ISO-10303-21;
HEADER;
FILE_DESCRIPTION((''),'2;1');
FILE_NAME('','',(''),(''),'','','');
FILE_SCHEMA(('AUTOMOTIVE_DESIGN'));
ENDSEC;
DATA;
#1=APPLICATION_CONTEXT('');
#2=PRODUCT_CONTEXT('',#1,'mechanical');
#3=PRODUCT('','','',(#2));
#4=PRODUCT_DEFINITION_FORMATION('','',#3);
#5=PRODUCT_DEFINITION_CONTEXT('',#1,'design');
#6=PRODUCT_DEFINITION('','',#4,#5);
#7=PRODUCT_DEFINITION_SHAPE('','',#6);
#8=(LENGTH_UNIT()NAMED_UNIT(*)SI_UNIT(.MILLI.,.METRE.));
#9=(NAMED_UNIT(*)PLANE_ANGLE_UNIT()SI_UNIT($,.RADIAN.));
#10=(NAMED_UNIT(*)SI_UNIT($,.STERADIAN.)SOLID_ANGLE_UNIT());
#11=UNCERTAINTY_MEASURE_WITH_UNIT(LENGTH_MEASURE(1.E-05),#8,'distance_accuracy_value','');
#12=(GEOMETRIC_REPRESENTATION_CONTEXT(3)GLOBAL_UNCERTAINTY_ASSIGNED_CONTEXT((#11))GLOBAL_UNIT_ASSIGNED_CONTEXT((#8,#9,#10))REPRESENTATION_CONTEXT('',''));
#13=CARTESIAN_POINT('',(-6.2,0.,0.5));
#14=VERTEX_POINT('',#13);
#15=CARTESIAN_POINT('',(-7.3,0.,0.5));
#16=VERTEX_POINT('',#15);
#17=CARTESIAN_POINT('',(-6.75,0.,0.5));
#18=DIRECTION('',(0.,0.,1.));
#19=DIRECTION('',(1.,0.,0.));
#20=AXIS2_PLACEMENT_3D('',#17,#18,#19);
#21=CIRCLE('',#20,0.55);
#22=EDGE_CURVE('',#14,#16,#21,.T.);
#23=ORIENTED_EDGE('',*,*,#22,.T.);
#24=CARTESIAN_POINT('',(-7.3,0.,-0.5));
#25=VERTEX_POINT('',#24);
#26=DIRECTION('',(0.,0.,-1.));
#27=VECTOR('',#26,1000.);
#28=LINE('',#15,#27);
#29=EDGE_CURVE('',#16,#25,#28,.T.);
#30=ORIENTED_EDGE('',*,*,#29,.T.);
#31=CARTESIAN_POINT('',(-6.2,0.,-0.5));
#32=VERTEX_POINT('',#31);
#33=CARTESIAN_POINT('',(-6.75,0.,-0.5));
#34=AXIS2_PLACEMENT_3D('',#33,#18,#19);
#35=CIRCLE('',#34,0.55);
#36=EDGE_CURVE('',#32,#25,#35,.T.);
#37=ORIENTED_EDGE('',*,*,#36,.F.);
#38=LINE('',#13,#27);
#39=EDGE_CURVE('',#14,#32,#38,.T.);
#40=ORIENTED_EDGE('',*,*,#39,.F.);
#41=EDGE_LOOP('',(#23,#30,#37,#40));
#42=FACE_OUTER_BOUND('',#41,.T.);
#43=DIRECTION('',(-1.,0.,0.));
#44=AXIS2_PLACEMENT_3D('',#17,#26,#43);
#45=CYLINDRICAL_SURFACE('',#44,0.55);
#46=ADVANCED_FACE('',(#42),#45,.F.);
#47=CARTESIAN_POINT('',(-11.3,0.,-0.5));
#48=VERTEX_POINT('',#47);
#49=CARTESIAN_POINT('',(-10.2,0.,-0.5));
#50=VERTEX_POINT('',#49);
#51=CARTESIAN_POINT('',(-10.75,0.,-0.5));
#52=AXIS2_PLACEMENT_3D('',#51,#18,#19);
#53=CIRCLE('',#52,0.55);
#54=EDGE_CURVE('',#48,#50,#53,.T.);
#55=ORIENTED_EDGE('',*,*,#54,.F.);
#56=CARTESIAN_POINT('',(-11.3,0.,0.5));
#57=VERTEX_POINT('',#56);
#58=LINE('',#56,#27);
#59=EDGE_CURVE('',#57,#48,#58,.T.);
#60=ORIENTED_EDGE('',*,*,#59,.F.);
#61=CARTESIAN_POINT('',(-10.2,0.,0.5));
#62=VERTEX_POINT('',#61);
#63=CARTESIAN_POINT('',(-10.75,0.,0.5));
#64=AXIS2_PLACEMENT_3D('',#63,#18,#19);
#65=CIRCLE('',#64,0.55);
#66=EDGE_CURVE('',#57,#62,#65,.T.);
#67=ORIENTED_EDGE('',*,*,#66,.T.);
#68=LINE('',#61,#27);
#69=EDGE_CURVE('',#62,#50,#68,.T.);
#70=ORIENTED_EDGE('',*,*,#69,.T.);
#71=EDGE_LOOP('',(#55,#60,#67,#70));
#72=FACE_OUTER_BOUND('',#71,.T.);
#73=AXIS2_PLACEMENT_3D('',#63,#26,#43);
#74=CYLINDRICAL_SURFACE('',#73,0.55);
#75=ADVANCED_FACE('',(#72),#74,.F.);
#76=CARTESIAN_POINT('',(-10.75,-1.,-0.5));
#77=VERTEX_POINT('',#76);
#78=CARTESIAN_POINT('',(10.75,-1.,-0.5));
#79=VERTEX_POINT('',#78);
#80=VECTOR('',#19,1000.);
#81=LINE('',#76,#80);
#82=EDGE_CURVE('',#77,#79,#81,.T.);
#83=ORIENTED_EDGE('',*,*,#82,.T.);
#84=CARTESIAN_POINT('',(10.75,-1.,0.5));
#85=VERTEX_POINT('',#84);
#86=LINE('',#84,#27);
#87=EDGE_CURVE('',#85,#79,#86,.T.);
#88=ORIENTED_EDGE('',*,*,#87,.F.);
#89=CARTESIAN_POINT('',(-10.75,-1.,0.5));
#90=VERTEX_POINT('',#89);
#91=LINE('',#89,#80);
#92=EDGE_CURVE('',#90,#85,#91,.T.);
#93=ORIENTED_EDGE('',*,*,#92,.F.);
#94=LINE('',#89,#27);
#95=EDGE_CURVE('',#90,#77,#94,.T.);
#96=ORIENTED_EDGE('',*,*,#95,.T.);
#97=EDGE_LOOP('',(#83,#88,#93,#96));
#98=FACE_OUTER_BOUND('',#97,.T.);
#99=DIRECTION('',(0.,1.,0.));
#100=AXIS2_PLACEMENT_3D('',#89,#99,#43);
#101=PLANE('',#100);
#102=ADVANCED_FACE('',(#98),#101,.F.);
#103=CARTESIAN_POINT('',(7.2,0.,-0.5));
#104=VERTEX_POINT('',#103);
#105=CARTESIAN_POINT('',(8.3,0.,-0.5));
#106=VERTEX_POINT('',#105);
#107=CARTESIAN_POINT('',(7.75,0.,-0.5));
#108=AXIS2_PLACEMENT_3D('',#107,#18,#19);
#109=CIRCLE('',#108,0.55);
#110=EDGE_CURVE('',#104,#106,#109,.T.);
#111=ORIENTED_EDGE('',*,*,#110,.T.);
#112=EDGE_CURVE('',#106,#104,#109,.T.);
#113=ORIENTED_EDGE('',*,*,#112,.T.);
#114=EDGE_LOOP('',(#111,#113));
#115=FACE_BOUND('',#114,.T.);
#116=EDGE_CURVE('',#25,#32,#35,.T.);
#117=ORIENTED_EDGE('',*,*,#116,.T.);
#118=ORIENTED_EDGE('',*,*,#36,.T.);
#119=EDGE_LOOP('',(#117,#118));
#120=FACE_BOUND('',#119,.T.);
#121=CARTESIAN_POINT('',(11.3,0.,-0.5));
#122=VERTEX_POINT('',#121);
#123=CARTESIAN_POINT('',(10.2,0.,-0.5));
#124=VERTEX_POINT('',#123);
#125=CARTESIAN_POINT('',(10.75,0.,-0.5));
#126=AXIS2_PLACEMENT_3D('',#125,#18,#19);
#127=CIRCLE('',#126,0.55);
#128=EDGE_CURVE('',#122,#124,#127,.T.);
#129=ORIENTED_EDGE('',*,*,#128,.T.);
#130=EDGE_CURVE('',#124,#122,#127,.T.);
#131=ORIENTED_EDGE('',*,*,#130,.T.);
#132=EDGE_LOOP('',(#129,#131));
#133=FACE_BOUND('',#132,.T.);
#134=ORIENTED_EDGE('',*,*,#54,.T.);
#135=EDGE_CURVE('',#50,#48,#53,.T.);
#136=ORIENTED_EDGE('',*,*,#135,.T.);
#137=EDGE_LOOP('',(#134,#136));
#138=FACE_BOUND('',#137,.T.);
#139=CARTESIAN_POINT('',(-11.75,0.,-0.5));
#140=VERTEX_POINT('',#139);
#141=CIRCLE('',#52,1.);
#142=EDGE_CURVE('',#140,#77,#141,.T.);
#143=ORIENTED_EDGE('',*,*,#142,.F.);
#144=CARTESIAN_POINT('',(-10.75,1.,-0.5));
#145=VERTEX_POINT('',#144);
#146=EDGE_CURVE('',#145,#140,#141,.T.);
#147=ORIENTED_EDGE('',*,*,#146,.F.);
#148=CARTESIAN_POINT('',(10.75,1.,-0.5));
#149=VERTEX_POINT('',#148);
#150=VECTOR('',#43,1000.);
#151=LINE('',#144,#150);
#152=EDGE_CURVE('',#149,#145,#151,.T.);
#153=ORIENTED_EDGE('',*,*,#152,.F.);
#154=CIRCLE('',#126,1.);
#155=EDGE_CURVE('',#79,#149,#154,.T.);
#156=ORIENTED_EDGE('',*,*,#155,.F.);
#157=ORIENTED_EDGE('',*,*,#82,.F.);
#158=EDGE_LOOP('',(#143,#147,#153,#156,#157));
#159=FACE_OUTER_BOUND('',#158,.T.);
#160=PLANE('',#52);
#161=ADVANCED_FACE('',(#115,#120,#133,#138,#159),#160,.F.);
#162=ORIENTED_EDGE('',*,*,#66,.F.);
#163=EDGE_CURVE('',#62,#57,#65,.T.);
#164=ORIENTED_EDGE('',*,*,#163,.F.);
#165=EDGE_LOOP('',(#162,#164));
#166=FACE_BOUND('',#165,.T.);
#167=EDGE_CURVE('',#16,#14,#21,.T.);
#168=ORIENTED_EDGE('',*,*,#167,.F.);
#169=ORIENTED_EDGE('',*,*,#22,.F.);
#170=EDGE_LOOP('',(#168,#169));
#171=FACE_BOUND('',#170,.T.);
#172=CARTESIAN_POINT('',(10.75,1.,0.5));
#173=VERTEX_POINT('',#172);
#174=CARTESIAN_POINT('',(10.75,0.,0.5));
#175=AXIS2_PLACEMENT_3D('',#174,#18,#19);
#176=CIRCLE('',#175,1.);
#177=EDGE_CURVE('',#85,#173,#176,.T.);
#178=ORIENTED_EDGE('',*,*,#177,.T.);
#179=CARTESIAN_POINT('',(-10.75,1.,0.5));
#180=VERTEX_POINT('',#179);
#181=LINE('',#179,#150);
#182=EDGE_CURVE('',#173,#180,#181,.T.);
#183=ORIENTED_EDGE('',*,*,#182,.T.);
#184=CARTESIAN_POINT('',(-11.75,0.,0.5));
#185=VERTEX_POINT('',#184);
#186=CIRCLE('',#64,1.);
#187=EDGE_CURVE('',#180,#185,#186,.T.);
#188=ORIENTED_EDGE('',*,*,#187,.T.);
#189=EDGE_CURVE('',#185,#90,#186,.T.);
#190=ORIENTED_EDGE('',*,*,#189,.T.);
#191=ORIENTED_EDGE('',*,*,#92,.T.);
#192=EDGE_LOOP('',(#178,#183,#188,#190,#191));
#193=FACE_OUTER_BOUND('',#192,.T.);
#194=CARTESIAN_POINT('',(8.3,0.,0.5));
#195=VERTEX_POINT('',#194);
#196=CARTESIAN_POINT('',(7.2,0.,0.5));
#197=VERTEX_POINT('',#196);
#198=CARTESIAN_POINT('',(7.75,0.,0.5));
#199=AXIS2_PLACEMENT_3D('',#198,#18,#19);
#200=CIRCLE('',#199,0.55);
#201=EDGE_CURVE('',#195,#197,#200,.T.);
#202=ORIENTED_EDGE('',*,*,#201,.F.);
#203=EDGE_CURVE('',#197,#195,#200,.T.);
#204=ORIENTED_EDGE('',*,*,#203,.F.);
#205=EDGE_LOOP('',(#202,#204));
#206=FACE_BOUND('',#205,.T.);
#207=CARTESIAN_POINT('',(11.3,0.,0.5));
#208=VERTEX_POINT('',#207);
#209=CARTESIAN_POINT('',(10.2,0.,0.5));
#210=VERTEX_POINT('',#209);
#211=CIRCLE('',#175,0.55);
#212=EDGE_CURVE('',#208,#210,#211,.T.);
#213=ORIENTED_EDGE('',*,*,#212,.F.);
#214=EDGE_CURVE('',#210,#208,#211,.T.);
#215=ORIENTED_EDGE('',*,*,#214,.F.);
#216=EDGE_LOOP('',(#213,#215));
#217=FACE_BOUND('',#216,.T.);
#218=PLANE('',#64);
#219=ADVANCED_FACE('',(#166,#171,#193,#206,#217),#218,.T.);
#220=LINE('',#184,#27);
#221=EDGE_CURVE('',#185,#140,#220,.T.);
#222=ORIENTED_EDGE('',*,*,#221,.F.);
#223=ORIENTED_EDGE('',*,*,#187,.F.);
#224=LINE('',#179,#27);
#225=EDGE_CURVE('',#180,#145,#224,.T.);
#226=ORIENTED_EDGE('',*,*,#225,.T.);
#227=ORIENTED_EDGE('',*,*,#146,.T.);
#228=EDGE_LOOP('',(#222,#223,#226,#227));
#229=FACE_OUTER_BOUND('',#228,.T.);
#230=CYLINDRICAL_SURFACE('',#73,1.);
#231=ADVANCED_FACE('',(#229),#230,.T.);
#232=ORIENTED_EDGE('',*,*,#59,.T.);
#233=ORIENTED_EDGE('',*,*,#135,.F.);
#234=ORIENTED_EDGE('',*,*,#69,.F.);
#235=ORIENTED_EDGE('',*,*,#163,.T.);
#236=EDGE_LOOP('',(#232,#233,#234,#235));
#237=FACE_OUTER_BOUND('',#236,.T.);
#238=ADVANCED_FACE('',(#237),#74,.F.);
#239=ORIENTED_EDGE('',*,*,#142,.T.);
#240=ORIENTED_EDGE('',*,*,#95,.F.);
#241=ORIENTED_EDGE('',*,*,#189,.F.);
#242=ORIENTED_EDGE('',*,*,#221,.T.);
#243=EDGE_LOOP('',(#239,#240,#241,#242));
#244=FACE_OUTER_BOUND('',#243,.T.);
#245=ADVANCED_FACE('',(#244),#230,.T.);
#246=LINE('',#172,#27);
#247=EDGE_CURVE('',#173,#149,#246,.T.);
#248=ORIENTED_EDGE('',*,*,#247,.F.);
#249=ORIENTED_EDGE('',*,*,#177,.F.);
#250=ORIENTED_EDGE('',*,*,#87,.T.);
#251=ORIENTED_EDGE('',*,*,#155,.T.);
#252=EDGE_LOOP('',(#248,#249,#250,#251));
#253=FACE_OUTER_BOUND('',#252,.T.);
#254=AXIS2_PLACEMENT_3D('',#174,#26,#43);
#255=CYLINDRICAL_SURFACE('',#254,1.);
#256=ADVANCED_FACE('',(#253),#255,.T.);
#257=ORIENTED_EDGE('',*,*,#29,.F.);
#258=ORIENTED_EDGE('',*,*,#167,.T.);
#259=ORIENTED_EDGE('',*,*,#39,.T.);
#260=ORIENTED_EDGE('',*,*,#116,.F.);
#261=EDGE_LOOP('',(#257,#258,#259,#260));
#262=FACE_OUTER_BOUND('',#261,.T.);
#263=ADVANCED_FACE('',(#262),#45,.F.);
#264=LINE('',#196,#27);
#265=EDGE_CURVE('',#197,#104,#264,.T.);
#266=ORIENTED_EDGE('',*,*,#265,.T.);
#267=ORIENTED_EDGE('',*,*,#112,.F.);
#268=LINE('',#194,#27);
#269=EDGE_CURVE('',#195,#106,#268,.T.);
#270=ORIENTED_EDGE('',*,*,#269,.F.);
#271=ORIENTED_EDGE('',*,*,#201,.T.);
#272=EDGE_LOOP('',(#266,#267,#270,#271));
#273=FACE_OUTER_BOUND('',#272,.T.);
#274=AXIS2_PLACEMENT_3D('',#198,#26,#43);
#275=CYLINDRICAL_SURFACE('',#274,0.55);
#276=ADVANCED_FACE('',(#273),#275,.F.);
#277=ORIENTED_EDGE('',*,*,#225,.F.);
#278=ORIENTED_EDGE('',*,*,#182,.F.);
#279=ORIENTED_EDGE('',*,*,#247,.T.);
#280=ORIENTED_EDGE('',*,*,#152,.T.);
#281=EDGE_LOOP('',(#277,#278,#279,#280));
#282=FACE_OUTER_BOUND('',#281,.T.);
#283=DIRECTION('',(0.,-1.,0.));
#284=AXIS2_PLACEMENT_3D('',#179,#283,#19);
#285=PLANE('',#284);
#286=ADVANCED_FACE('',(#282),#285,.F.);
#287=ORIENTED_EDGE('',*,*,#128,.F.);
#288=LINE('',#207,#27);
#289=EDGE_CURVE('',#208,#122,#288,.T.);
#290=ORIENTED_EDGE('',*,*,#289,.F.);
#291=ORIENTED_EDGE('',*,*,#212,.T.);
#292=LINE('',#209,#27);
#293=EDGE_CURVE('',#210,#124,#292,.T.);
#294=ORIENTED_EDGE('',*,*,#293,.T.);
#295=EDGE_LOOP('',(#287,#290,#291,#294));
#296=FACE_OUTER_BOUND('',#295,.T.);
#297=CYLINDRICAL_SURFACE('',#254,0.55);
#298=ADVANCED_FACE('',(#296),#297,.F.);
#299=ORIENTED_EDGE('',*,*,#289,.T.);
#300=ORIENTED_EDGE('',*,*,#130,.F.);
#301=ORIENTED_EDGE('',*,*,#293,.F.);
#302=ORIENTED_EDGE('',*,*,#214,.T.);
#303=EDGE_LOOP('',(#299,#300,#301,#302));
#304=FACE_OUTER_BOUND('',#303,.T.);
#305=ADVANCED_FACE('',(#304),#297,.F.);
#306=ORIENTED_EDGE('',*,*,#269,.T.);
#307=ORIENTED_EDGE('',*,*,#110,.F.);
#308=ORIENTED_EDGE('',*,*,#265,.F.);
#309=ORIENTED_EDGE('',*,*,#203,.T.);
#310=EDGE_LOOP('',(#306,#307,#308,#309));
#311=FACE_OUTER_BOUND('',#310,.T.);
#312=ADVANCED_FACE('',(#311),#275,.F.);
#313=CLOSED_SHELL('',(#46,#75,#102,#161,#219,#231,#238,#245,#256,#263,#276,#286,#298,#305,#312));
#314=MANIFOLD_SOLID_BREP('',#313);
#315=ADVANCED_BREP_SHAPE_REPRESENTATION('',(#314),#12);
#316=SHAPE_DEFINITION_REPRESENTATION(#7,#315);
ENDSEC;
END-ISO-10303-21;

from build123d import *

# Parameters (mm, degrees)
SKETCH1_R           = 0.55
THIGH1_LENGTH_DEPTH = 0.5


with BuildPart() as part:
    # Sketch1 → Thigh1 length (new, symmetric)
    with BuildSketch(Plane.XY):
        with BuildLine():
            Line((-10.75, 1), (10.75, 1))
            ThreePointArc((10.75, 1), (11.75, 0), (10.75, -1))
            Line((10.75, -1), (-10.75, -1))
            ThreePointArc((-10.75, -1), (-11.75, 0), (-10.75, 1))
        make_face()
        with Locations((-10.75, 0)):
            Circle(SKETCH1_R, mode=Mode.SUBTRACT)
        with Locations((10.75, 0)):
            Circle(SKETCH1_R, mode=Mode.SUBTRACT)
        with Locations((-6.75, 0)):
            Circle(SKETCH1_R, mode=Mode.SUBTRACT)
        with Locations((7.75, 0)):
            Circle(SKETCH1_R, mode=Mode.SUBTRACT)
    extrude(amount=THIGH1_LENGTH_DEPTH, both=True)


solid = part.part
